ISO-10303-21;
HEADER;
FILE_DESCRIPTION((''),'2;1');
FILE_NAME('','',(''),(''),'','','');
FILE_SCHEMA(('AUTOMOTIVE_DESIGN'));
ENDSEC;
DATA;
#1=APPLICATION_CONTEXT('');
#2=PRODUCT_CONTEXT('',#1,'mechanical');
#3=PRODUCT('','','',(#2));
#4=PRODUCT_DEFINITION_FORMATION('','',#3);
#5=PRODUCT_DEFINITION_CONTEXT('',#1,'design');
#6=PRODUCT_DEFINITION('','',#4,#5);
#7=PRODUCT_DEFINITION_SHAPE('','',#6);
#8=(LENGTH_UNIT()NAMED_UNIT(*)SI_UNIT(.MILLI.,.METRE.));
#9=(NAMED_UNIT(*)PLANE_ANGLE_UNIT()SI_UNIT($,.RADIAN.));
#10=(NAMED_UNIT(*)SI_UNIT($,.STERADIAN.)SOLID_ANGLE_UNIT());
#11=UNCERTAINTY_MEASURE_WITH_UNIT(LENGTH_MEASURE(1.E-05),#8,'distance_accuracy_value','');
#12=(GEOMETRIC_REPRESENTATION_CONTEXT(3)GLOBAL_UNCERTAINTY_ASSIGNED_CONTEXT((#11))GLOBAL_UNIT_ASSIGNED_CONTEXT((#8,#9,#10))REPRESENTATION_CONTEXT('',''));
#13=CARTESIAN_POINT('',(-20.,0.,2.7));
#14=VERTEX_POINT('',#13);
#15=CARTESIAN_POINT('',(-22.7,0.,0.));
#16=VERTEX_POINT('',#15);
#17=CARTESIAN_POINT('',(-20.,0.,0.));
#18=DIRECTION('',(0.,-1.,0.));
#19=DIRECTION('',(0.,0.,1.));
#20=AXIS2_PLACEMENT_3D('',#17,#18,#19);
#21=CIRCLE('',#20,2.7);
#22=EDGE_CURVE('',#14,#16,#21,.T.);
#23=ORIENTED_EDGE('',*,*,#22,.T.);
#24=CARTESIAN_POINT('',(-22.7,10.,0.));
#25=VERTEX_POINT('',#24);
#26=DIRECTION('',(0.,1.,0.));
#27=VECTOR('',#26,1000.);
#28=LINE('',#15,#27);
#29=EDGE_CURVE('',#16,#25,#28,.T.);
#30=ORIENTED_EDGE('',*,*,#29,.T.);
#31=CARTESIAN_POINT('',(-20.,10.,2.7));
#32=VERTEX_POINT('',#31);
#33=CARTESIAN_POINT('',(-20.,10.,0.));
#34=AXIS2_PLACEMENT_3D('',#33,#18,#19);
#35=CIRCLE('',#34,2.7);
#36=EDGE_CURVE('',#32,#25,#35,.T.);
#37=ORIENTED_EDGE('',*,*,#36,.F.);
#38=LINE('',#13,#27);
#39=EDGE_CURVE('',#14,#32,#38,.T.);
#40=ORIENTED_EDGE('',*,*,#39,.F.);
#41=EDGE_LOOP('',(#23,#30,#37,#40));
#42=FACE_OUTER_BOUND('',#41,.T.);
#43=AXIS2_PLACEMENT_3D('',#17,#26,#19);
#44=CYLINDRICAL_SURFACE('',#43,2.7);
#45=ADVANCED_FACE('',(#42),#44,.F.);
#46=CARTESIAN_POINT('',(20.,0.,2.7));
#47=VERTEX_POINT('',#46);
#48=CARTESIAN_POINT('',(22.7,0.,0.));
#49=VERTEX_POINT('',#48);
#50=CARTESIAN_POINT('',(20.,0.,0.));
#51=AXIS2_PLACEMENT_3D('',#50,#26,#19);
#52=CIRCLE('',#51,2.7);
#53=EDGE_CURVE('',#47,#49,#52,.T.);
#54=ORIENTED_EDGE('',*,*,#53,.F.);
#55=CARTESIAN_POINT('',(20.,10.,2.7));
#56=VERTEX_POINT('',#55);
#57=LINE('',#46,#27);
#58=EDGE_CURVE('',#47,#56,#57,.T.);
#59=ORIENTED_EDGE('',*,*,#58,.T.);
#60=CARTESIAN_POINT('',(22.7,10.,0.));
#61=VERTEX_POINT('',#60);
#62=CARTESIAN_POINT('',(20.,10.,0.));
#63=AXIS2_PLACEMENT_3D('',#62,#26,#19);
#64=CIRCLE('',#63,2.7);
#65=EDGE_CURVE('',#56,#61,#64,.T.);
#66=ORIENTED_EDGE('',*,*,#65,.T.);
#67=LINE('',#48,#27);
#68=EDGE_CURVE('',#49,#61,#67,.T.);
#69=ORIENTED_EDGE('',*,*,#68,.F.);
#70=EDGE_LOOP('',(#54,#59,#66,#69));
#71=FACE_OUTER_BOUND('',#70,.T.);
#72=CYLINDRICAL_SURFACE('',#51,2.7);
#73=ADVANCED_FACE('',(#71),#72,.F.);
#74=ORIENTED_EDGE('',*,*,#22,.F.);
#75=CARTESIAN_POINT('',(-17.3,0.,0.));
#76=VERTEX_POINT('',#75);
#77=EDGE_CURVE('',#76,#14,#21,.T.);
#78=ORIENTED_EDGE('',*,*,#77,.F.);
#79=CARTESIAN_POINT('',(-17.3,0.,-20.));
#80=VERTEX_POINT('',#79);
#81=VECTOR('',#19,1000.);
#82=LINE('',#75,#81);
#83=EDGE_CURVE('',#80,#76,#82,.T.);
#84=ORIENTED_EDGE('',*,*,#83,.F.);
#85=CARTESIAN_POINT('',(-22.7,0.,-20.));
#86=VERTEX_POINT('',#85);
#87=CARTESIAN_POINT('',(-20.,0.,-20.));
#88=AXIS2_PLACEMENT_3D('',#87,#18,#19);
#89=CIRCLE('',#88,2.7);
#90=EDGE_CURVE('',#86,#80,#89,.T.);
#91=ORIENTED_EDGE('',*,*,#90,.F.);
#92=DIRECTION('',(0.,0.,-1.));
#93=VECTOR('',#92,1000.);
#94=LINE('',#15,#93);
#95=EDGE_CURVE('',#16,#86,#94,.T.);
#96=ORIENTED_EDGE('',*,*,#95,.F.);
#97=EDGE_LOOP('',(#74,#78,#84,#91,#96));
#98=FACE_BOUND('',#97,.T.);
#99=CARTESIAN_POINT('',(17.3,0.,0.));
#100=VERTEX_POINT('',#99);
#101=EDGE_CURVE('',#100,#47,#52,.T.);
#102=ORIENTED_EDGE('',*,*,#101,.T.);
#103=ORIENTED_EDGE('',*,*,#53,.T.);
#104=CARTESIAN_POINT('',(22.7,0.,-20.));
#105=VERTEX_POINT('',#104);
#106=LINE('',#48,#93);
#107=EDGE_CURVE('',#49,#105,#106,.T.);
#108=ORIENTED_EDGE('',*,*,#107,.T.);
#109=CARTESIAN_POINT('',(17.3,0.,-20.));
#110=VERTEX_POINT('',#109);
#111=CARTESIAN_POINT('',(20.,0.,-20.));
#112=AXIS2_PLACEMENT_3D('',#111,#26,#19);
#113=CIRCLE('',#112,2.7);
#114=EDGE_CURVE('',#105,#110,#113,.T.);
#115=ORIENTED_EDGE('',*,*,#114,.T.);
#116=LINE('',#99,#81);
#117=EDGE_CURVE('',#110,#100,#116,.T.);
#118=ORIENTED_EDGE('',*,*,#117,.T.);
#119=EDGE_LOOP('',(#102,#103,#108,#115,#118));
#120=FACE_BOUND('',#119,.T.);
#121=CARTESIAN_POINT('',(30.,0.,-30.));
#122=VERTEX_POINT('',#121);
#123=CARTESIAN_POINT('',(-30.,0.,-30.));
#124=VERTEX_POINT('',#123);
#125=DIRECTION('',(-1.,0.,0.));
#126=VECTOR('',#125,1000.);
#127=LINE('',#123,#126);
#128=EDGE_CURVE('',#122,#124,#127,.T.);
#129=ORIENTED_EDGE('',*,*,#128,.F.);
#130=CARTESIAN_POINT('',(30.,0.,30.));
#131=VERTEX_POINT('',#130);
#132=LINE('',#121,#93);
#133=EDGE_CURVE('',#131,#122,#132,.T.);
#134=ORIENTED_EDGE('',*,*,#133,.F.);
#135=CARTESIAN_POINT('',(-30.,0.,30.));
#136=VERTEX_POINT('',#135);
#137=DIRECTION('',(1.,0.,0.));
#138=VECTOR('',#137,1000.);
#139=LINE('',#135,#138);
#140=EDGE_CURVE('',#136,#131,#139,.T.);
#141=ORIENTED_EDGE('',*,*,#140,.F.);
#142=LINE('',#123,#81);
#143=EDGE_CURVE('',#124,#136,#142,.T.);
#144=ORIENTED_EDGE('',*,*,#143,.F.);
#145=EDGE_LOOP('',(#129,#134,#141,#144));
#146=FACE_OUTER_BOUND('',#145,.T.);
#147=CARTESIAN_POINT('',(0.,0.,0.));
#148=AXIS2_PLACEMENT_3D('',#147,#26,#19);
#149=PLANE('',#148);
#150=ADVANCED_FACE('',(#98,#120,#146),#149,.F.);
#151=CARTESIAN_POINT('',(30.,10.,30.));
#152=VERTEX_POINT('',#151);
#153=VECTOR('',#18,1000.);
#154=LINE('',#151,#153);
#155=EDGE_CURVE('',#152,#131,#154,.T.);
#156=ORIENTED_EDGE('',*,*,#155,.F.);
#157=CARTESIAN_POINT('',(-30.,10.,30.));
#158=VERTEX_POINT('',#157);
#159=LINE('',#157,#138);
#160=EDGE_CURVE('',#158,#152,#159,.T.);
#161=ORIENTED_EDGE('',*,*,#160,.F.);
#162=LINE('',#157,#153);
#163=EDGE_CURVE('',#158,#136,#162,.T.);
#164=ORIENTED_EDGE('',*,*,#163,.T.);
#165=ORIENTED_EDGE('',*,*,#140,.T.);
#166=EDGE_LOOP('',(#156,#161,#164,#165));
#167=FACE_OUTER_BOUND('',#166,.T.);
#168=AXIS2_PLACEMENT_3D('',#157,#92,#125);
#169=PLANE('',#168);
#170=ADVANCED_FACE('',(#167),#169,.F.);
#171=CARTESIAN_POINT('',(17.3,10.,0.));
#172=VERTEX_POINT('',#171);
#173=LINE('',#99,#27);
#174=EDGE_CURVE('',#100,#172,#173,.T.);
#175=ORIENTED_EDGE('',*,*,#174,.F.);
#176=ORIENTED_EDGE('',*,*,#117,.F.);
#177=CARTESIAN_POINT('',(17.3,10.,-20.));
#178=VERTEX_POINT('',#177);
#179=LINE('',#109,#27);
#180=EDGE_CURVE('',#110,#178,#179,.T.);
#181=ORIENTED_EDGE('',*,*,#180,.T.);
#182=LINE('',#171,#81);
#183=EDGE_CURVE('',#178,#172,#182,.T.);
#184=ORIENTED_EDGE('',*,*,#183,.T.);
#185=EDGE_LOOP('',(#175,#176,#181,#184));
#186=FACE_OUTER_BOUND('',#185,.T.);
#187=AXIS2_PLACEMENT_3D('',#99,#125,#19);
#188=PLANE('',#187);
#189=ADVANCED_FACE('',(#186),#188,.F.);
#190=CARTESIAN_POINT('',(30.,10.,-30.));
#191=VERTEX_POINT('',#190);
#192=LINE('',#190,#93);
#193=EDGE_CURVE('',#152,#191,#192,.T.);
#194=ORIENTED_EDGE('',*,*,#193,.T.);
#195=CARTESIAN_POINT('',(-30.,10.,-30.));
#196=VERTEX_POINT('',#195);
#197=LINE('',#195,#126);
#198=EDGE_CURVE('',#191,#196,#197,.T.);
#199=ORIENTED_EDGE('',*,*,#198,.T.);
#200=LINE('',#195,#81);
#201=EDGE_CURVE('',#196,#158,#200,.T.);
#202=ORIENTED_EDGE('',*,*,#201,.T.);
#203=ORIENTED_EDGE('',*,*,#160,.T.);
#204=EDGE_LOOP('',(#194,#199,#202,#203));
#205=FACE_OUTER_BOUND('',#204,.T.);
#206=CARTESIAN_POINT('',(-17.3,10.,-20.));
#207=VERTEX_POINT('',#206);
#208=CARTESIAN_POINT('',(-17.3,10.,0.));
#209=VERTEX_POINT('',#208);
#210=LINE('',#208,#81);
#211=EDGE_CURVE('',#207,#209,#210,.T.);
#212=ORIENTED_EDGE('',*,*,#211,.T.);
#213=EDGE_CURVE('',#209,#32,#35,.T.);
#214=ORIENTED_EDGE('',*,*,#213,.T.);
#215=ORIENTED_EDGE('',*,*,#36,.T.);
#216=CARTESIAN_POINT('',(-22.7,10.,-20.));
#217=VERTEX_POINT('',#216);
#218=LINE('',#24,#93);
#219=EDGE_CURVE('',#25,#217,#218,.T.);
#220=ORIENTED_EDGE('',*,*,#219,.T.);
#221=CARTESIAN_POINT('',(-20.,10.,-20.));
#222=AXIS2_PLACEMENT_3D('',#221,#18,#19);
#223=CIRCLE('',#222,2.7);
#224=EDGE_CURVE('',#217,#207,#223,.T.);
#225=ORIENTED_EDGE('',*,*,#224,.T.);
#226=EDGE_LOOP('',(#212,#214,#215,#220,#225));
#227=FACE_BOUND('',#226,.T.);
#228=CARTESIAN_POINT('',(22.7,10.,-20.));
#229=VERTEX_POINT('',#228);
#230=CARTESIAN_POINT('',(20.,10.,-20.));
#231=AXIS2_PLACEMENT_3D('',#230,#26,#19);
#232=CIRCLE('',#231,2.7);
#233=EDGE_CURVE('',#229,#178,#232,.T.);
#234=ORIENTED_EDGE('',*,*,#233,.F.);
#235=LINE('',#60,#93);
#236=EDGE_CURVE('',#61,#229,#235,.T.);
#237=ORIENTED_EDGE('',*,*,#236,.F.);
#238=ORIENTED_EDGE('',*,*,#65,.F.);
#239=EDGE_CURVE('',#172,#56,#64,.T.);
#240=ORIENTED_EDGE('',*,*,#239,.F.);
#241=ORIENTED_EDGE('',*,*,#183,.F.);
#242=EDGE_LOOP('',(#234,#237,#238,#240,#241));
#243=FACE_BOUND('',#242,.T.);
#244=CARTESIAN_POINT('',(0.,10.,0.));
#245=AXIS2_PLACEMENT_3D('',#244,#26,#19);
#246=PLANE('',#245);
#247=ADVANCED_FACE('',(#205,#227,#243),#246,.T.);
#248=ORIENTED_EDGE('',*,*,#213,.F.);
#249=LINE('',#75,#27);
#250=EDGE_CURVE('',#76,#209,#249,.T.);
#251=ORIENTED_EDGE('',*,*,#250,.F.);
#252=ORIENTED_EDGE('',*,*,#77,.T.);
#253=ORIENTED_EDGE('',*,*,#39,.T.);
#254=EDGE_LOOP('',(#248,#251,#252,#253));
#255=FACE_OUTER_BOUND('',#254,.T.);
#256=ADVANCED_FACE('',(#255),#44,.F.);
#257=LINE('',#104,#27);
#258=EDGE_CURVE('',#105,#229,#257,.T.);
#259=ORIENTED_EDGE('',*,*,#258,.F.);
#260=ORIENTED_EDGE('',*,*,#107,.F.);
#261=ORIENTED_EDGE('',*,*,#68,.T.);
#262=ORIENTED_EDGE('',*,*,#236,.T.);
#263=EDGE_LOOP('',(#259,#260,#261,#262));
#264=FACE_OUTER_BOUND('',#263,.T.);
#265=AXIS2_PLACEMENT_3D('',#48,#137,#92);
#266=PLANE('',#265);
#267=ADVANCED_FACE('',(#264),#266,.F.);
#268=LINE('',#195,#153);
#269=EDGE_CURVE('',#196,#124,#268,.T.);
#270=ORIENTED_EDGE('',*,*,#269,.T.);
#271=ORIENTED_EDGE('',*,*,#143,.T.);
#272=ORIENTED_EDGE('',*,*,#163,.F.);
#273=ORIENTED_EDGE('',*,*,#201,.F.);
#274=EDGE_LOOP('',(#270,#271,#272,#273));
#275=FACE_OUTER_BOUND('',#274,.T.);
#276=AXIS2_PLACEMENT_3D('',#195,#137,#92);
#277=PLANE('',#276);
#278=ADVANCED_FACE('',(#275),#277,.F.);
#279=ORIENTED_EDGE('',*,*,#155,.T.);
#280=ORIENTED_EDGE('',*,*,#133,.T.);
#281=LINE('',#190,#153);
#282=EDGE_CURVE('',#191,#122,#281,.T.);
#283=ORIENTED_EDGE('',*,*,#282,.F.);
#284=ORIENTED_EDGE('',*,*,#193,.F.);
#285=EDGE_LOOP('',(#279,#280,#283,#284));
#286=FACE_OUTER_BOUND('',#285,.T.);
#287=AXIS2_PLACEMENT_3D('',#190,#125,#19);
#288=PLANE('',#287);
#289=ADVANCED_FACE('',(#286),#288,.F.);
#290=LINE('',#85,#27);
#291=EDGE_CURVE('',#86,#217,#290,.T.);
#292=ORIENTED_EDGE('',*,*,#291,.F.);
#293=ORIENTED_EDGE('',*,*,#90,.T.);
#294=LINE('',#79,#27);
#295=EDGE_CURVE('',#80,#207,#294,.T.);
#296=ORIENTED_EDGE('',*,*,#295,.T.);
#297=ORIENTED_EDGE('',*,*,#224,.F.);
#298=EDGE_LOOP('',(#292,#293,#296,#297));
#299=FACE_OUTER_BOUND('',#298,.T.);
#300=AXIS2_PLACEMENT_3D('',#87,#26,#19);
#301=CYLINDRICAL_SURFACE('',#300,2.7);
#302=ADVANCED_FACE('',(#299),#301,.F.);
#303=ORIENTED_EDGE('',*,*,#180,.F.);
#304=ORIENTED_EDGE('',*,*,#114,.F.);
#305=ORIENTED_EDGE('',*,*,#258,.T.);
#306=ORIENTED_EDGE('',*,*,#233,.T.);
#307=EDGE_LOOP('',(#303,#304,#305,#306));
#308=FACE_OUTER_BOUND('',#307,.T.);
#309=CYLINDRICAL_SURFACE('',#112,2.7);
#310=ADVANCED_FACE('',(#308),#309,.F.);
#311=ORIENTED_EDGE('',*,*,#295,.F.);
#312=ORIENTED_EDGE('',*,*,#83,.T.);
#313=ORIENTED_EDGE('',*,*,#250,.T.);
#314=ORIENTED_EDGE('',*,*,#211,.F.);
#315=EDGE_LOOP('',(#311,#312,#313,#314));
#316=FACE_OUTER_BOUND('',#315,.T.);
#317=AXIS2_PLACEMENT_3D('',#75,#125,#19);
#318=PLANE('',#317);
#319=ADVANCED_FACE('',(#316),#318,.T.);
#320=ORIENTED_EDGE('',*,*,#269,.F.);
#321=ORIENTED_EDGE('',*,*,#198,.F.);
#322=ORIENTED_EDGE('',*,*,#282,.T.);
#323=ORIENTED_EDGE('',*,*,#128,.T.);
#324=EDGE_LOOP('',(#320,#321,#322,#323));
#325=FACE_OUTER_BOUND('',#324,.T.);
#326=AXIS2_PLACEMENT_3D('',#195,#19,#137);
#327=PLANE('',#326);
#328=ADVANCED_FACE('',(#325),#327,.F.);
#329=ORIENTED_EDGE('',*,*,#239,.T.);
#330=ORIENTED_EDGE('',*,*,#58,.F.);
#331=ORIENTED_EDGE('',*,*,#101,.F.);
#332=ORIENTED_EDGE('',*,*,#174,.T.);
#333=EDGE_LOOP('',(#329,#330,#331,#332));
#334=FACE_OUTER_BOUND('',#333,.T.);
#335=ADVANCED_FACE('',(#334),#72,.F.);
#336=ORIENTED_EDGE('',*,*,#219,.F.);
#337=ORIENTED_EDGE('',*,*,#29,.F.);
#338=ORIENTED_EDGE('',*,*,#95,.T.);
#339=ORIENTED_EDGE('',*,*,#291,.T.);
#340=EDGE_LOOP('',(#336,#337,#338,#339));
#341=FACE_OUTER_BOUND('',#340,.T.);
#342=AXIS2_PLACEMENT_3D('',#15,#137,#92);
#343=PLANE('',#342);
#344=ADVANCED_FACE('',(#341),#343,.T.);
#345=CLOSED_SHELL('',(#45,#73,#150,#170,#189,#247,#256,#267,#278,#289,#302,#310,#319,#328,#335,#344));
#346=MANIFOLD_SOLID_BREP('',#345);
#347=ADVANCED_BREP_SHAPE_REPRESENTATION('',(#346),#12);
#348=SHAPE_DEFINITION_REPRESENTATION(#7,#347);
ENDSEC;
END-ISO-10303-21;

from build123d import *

# Parameters (mm, degrees)
SKETCH1_W           = 60
SKETCH1_H           = 60
BOSS_EXTRUDE1_DEPTH = 10
CUT_EXTRUDE1_DEPTH  = 44.588989435


with BuildPart() as part:
    # Sketch1 → Boss-Extrude1 (new body)
    with BuildSketch(Plane(origin=(0, 0, 0), x_dir=(1, 0, 0), z_dir=(0, 1, 0))):
        Rectangle(SKETCH1_W, SKETCH1_H)
    extrude(amount=BOSS_EXTRUDE1_DEPTH)

    # Sketch2 → Cut-Extrude1 (cut, through all)
    with BuildSketch(Plane(origin=(0, 10, 0), x_dir=(1, 0, 0), z_dir=(0, 1, 0))):
        with BuildLine():
            Line((17.3, 0), (17.3, 20))
            ThreePointArc((17.3, 20), (20, 22.7), (22.7, 20))
            Line((22.7, 20), (22.7, 0))
            ThreePointArc((22.7, 0), (20, -2.7), (17.3, 0))
        make_face()
    cut_extrude1 = extrude(amount=-CUT_EXTRUDE1_DEPTH, mode=Mode.SUBTRACT)

    # Mirror1: Cut-Extrude1 across plane
    add(cut_extrude1.mirror(Plane(origin=(0, 0, 0), x_dir=(0, 0, 1), z_dir=(1, 0, 0))), mode=Mode.SUBTRACT)


solid = part.part
